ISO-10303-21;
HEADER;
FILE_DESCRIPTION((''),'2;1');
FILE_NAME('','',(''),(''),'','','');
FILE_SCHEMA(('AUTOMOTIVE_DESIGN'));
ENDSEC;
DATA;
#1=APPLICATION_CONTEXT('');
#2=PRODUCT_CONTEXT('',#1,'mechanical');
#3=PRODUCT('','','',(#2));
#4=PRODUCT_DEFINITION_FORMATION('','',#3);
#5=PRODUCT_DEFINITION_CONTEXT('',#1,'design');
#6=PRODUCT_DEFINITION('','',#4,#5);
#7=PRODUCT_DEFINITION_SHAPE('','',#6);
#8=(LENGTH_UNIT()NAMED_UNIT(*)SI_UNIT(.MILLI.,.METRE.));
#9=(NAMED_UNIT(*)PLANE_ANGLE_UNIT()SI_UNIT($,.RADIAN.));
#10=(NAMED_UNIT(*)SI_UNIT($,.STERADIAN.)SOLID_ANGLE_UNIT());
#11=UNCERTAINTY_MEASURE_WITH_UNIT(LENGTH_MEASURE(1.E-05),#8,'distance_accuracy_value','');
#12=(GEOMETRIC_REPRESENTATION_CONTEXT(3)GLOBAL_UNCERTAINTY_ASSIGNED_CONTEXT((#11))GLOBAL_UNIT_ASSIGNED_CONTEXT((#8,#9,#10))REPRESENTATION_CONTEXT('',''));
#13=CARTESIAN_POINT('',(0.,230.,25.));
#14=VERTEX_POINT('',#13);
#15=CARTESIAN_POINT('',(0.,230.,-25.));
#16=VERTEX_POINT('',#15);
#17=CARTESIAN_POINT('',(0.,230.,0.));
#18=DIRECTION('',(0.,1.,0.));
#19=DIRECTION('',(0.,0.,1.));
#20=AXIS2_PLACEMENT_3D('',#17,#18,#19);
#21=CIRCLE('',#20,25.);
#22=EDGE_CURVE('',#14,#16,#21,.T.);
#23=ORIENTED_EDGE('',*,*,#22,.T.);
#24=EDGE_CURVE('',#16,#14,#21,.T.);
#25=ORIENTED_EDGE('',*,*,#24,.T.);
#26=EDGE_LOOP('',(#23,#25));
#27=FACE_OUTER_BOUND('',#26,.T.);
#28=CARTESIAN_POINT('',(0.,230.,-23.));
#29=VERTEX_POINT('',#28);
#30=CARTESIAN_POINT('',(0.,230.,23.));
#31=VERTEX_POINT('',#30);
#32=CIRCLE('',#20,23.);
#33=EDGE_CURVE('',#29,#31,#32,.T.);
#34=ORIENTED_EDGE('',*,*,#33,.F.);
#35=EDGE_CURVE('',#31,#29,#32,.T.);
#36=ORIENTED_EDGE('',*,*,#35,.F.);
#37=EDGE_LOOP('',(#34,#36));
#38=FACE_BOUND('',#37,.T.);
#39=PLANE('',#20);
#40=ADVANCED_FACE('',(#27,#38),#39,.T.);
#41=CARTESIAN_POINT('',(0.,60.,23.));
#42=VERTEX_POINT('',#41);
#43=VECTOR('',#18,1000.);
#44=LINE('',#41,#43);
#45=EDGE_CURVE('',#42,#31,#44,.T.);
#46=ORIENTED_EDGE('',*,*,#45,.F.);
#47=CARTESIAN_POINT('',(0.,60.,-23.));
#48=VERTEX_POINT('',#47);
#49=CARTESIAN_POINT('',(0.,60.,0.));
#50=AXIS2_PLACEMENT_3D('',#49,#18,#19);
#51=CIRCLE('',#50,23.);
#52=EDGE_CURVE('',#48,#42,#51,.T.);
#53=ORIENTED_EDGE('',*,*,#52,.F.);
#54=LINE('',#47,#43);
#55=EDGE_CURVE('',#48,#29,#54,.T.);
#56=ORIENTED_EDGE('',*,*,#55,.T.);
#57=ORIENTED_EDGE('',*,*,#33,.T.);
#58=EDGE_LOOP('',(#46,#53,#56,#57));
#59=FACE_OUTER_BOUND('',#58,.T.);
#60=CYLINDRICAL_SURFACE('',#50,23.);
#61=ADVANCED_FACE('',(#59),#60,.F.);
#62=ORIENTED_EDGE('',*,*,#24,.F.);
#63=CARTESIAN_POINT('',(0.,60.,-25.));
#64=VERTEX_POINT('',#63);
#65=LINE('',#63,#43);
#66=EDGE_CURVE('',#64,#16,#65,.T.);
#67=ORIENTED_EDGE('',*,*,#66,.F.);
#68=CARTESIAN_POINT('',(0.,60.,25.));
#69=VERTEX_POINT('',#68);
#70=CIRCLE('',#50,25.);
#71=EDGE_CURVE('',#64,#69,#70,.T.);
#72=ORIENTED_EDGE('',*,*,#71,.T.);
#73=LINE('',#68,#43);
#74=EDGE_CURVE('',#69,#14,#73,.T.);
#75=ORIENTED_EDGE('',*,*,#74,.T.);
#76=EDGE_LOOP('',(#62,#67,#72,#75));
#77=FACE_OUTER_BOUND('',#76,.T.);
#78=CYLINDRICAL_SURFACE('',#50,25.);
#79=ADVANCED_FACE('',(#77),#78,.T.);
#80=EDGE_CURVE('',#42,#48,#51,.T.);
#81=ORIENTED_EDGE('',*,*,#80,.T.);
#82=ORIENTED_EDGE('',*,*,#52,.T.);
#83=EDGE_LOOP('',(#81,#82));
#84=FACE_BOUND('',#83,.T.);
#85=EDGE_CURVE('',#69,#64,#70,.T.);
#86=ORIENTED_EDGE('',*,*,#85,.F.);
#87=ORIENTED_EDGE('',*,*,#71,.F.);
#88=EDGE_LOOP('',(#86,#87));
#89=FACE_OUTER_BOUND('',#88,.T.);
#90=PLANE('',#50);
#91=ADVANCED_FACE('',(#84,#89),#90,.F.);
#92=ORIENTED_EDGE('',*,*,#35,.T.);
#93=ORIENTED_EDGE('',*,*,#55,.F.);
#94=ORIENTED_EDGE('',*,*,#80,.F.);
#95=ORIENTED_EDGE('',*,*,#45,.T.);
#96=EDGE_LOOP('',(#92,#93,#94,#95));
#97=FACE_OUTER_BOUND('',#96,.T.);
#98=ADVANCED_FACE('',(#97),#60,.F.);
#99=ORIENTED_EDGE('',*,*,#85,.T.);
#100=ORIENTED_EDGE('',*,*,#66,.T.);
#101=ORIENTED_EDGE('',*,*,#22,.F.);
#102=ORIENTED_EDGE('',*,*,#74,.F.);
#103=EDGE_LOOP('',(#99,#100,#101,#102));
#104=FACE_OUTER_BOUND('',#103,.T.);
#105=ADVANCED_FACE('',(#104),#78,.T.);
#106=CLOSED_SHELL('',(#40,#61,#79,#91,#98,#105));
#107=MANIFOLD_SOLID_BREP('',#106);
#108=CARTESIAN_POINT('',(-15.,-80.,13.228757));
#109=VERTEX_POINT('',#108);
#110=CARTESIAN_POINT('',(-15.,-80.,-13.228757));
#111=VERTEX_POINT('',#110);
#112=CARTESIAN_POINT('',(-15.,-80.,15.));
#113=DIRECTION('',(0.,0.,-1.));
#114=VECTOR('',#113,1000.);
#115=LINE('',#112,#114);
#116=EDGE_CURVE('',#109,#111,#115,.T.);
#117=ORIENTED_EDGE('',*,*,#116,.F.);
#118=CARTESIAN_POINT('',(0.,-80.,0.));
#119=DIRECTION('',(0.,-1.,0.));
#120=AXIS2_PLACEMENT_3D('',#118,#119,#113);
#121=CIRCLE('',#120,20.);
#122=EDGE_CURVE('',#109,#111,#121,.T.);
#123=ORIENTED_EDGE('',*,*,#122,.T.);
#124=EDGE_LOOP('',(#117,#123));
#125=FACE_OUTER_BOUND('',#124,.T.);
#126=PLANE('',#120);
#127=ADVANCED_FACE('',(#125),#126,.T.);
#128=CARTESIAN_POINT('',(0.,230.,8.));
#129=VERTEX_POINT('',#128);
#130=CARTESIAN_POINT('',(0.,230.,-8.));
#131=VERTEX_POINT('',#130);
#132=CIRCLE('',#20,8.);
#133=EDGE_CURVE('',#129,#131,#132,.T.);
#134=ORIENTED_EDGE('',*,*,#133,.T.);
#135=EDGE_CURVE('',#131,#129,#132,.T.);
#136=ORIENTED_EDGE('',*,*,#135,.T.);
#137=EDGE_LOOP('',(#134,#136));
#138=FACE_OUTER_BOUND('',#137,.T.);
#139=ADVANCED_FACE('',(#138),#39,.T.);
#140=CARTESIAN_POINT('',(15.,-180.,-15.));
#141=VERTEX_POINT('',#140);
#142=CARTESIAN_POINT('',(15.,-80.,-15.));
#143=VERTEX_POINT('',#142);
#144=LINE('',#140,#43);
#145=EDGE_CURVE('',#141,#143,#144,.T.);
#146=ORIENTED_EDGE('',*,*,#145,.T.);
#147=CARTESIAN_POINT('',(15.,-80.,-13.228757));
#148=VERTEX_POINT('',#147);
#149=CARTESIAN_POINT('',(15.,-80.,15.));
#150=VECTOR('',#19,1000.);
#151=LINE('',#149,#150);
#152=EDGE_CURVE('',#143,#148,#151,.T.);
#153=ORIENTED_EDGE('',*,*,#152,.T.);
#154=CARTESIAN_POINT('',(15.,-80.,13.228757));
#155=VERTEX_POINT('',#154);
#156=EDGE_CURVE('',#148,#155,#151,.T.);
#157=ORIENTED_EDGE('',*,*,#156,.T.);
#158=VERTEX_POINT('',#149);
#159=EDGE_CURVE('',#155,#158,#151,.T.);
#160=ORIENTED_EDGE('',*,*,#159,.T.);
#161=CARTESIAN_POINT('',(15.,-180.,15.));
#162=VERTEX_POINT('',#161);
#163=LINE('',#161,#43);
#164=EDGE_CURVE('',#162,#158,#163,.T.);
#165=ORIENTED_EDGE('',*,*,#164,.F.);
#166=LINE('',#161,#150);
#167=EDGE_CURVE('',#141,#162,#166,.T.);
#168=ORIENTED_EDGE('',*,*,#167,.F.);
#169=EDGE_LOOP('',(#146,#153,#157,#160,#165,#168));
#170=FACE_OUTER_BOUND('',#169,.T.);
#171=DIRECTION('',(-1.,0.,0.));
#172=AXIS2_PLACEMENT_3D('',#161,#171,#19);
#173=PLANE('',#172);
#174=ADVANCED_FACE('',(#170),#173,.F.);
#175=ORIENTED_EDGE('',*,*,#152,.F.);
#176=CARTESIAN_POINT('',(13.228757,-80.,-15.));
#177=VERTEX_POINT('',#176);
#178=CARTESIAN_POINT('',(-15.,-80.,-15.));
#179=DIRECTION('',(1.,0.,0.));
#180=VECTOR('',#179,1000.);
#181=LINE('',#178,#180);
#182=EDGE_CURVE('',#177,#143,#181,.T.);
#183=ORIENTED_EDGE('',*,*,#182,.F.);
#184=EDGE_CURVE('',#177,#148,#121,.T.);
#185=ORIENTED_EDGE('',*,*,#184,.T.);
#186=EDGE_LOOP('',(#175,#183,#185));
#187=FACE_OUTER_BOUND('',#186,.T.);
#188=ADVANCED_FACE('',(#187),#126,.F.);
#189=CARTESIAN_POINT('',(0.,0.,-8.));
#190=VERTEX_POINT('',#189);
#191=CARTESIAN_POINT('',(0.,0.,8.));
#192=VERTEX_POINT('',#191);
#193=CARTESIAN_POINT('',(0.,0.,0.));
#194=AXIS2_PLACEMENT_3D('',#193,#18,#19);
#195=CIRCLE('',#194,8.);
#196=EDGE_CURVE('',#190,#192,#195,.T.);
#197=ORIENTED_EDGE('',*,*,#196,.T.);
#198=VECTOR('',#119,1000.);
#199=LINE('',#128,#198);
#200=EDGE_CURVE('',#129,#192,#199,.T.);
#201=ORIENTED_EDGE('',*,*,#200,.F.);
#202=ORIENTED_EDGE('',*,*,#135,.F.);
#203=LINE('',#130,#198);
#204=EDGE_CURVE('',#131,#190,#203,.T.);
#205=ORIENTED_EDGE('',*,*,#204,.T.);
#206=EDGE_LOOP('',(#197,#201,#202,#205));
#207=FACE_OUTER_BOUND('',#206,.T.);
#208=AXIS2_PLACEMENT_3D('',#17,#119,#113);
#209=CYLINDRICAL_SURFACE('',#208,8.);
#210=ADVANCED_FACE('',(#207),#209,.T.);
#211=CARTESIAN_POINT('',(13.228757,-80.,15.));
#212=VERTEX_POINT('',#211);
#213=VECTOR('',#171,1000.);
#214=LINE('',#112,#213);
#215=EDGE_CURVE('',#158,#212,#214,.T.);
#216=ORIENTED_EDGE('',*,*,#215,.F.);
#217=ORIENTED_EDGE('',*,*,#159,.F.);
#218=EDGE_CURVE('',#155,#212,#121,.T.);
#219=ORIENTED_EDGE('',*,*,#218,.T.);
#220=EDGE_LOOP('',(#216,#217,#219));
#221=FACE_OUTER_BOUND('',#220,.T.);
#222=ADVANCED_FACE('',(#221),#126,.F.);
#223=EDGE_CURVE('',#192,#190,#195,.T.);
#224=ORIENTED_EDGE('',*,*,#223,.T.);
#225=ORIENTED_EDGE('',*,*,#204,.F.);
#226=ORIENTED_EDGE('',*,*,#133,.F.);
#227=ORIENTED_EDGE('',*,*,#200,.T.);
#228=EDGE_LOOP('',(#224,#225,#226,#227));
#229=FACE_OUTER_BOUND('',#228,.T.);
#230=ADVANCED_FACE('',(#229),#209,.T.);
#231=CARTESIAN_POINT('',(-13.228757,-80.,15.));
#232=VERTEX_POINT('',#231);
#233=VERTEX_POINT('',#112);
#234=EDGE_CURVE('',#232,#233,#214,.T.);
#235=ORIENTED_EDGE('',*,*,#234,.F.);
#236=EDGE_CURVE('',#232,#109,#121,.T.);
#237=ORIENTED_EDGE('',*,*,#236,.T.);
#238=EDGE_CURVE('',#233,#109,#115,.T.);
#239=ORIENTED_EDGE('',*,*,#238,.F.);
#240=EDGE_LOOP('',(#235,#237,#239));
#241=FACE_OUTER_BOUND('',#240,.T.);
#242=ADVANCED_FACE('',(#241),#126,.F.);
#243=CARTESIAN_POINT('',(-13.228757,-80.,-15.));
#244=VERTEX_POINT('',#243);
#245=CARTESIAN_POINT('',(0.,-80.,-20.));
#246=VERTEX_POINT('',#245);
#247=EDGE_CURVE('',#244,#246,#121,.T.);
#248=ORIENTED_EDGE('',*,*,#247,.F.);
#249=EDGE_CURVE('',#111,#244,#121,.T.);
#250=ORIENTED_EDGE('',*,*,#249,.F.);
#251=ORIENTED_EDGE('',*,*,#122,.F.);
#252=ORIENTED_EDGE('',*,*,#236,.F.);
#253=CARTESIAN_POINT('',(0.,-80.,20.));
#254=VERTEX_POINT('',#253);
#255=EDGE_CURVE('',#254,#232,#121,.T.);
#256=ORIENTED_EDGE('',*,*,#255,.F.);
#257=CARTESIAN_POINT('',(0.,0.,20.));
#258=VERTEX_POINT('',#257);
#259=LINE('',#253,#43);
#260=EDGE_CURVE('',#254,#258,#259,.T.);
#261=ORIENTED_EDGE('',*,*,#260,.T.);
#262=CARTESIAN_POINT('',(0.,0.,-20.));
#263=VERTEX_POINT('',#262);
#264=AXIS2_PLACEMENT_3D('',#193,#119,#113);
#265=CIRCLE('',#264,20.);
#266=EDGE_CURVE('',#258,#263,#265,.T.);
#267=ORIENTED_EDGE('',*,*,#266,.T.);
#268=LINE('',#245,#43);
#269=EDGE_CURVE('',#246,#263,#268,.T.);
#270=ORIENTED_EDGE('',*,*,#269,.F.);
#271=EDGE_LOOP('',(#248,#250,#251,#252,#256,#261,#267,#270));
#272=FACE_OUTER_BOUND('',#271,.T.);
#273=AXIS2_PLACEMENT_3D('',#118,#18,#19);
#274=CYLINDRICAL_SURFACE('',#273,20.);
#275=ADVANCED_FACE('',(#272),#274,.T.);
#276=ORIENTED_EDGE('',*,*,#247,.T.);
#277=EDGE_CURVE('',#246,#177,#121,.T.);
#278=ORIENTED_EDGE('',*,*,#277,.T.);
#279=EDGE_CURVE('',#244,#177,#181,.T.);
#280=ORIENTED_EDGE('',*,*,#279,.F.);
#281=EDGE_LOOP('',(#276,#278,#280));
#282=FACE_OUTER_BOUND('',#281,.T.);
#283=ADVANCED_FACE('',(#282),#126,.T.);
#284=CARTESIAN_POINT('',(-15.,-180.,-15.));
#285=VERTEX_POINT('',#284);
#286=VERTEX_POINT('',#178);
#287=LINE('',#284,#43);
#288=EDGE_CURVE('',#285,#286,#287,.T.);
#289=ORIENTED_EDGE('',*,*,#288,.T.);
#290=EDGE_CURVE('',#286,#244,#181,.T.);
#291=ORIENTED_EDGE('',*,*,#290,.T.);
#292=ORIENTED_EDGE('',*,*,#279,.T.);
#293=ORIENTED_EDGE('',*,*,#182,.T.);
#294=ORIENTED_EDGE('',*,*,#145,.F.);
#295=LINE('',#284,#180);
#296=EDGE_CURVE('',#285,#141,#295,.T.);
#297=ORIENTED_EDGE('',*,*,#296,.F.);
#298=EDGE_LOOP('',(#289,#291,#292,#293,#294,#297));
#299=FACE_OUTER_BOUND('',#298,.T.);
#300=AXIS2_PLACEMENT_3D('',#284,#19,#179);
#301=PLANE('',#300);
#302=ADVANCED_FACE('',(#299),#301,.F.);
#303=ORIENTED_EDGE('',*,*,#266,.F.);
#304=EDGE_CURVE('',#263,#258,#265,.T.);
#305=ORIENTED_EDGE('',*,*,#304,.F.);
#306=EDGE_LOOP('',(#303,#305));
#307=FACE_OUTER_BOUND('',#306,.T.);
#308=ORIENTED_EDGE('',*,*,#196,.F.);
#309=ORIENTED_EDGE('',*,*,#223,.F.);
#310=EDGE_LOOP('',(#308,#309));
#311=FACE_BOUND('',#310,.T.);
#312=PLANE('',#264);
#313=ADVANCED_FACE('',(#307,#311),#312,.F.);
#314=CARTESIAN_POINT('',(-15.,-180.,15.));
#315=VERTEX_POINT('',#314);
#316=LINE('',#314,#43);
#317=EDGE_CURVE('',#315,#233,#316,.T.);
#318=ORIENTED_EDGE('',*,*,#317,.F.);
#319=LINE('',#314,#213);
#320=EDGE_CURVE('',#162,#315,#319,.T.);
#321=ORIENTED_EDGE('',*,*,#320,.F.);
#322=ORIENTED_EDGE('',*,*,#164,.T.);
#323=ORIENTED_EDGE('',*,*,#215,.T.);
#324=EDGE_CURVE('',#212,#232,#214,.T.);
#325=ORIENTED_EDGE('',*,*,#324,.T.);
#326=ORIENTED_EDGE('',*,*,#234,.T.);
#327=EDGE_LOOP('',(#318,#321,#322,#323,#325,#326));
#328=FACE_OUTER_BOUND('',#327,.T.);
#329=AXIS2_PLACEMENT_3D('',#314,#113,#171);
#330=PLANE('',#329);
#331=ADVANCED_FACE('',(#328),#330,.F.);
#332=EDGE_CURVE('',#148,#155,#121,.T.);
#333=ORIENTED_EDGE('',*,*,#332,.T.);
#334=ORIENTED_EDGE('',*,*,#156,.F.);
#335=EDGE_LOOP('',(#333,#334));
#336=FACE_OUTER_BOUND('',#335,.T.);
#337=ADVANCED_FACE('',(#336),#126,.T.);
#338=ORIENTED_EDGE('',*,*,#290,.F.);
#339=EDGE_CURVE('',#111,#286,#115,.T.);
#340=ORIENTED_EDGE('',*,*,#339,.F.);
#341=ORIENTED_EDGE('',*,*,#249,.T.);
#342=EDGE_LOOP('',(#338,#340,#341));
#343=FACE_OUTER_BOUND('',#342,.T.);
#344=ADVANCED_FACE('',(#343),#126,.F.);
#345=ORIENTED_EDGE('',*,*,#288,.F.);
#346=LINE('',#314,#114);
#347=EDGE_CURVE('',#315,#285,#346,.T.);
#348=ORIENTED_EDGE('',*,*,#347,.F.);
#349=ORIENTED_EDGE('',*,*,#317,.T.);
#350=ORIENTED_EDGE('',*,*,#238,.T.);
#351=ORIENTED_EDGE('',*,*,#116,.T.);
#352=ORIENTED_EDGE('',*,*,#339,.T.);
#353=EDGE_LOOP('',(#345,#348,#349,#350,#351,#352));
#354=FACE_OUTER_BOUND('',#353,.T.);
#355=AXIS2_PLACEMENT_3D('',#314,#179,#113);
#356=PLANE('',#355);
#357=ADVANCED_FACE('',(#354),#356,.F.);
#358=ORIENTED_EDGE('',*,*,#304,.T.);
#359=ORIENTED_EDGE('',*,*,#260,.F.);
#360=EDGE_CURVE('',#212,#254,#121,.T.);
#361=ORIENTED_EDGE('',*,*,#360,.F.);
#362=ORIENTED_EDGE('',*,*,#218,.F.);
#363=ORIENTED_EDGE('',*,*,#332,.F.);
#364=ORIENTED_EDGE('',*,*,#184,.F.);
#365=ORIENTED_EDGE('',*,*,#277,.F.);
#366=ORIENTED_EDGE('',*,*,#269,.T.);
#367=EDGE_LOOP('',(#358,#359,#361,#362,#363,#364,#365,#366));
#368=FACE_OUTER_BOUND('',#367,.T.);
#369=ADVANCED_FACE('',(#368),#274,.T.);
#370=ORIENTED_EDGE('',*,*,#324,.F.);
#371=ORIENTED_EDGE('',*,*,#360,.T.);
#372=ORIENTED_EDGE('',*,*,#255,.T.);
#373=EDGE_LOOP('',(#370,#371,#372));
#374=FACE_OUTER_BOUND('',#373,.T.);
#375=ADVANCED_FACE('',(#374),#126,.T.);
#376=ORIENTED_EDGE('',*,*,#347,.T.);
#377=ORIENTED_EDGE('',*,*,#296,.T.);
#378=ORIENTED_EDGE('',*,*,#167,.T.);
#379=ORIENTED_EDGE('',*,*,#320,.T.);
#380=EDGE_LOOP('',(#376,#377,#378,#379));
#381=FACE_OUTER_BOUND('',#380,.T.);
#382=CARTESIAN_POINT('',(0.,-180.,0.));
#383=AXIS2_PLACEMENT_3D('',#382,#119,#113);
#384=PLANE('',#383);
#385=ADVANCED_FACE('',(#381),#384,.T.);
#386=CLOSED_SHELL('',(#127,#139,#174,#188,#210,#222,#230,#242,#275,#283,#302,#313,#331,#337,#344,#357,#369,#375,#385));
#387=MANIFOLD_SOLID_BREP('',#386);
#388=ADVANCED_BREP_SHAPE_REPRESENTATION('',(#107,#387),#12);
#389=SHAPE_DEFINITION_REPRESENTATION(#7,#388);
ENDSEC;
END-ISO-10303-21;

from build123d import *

# Parameters (mm, degrees)
SKETCH1_R           = 8
BOSS_EXTRUDE1_DEPTH = 230
SKETCH3_R           = 25
SKETCH3_R_2         = 23
BOSS_EXTRUDE2_DEPTH = 170
BOSS_EXTRUDE3_START = 80
SKETCH4_W           = 30
SKETCH4_H           = 30
BOSS_EXTRUDE3_DEPTH = 100
SKETCH5_R           = 20
BOSS_EXTRUDE4_DEPTH = 80


with BuildPart() as part:
    # Sketch1 → Boss-Extrude1 (new body)
    with BuildSketch(Plane(origin=(0, 0, 0), x_dir=(1, 0, 0), z_dir=(0, 1, 0))):
        with Locations(Location((0, 0, 0), (0, 0, 270))):
            Circle(SKETCH1_R)
    extrude(amount=BOSS_EXTRUDE1_DEPTH)



with BuildPart() as body_2:
    # Sketch3 → Boss-Extrude2 (new body)
    with BuildSketch(Plane(origin=(0, 230, 0), x_dir=(1, 0, 0), z_dir=(0, 1, 0))):
        with Locations(Location((0, 0, 0), (0, 0, 270))):
            Circle(SKETCH3_R)
        with Locations(Location((0, 0, 0), (0, 0, 270))):
            Circle(SKETCH3_R_2, mode=Mode.SUBTRACT)
    extrude(amount=-BOSS_EXTRUDE2_DEPTH)


with BuildPart() as body_3:
    # Sketch4 → Boss-Extrude3 (new body)
    with BuildSketch(Plane.XZ.offset(BOSS_EXTRUDE3_START)):
        Rectangle(SKETCH4_W, SKETCH4_H)
    extrude(amount=BOSS_EXTRUDE3_DEPTH)


with BuildPart() as part_1:
    add(part.part)

    add(body_3.part)  # Boss-Extrude4 merges body 3
    # Sketch5 → Boss-Extrude4 (add)
    with BuildSketch(Plane.XZ):
        with Locations(Location((0, 0, 0), (0, 0, 131.409622109))):
            Circle(SKETCH5_R)
    extrude(amount=BOSS_EXTRUDE4_DEPTH)


solid = Compound([body_2.part, part_1.part])
